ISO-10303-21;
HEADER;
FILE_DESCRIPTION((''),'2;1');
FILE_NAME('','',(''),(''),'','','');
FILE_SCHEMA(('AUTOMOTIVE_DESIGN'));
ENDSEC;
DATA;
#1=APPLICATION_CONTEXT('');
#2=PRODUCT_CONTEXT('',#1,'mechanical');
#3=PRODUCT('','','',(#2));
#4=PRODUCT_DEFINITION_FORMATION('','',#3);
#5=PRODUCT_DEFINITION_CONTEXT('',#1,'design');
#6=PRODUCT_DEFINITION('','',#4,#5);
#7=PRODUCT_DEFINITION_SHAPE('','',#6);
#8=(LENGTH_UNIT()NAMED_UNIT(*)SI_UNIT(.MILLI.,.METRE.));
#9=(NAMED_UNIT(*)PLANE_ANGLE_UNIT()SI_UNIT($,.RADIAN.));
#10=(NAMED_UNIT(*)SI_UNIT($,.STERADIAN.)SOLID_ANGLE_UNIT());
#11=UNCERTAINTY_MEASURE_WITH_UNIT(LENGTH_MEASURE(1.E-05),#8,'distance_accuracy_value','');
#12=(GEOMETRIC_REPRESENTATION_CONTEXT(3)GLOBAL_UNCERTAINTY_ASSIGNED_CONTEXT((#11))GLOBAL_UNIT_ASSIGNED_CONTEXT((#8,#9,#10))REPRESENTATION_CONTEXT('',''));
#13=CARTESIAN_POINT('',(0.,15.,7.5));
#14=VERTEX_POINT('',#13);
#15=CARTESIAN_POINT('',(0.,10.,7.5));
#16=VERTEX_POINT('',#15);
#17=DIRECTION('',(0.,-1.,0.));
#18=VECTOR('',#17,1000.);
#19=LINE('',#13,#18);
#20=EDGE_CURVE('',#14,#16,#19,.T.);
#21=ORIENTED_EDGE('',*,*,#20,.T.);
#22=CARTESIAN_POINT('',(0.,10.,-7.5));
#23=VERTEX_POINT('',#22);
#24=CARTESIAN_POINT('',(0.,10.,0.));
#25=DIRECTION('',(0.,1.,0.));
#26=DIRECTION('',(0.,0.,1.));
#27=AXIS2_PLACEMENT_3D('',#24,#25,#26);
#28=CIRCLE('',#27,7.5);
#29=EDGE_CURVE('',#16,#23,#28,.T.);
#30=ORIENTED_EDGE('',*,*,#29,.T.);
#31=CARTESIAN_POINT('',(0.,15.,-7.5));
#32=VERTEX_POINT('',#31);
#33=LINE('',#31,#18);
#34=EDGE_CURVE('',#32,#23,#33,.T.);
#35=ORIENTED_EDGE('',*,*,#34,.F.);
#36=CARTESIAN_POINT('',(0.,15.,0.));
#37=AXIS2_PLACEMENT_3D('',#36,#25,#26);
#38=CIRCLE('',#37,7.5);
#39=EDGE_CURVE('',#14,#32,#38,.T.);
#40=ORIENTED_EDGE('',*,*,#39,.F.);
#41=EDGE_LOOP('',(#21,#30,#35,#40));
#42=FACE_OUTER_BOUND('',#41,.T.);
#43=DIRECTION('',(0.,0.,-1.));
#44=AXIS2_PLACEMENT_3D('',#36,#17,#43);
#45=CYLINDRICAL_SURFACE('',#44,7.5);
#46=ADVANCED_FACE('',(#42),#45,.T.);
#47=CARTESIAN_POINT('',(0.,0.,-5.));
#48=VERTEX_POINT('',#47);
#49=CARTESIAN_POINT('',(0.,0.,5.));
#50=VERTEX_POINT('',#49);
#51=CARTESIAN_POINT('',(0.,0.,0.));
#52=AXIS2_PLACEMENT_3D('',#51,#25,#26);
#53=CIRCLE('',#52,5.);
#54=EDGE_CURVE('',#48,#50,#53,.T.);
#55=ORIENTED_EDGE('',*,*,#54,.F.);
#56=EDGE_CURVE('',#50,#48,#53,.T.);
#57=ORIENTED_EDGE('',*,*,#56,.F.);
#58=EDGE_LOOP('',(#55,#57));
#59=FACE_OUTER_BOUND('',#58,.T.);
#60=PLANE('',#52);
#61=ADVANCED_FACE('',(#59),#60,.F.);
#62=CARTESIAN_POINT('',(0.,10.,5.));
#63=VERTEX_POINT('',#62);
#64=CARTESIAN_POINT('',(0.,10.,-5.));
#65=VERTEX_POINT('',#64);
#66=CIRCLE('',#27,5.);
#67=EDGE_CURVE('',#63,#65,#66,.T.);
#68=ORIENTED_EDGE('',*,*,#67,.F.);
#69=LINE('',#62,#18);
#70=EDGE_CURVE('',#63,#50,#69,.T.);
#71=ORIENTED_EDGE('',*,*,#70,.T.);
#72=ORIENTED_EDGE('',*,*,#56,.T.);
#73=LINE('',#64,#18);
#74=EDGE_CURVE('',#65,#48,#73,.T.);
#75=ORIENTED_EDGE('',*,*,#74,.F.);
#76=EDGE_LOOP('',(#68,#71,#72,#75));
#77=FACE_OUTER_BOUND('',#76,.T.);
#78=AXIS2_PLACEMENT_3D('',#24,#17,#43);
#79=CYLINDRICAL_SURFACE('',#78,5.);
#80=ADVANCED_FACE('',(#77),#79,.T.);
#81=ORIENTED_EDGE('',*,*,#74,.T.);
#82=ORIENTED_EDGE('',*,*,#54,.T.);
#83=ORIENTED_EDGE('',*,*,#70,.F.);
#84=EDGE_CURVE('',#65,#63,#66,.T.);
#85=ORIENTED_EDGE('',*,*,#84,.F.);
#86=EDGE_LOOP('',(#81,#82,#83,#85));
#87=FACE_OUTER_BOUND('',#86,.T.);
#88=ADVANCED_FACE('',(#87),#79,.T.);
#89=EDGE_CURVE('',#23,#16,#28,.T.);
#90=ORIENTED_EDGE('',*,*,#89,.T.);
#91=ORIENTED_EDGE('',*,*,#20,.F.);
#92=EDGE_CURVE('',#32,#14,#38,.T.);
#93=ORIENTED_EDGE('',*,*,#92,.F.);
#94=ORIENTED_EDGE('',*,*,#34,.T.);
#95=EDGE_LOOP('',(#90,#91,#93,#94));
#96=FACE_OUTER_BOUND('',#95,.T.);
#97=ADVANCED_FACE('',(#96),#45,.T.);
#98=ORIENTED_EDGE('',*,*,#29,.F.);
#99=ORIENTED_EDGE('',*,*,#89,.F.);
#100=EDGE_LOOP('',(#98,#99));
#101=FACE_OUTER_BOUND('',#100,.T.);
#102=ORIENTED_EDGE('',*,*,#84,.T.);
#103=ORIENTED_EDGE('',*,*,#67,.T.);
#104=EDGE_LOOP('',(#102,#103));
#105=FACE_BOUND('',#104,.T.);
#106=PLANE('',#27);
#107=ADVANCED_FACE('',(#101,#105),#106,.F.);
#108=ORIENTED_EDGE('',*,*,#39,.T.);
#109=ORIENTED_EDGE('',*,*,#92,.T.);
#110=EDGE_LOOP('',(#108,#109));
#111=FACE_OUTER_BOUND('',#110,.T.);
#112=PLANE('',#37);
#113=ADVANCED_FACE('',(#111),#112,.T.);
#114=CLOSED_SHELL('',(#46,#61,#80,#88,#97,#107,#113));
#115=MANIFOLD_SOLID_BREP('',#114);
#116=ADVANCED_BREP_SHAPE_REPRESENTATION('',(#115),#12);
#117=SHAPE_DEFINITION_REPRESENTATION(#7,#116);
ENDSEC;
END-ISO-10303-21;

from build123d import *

# Parameters (mm, degrees)
SKETCH1_R           = 5
BOSS_EXTRUDE1_DEPTH = 10
SKETCH2_R           = 7.5
BOSS_EXTRUDE2_DEPTH = 5


with BuildPart() as part:
    # Sketch1 → Boss-Extrude1 (new body)
    with BuildSketch(Plane(origin=(0, 0, 0), x_dir=(1, 0, 0), z_dir=(0, 1, 0))):
        with Locations(Location((0, 0, 0), (0, 0, 270))):
            Circle(SKETCH1_R)
    extrude(amount=BOSS_EXTRUDE1_DEPTH)

    # Sketch2 → Boss-Extrude2 (add)
    with BuildSketch(Plane(origin=(0, 10, 0), x_dir=(1, 0, 0), z_dir=(0, 1, 0))):
        with Locations(Location((0, 0, 0), (0, 0, 270))):
            Circle(SKETCH2_R)
    extrude(amount=BOSS_EXTRUDE2_DEPTH)


solid = part.part
